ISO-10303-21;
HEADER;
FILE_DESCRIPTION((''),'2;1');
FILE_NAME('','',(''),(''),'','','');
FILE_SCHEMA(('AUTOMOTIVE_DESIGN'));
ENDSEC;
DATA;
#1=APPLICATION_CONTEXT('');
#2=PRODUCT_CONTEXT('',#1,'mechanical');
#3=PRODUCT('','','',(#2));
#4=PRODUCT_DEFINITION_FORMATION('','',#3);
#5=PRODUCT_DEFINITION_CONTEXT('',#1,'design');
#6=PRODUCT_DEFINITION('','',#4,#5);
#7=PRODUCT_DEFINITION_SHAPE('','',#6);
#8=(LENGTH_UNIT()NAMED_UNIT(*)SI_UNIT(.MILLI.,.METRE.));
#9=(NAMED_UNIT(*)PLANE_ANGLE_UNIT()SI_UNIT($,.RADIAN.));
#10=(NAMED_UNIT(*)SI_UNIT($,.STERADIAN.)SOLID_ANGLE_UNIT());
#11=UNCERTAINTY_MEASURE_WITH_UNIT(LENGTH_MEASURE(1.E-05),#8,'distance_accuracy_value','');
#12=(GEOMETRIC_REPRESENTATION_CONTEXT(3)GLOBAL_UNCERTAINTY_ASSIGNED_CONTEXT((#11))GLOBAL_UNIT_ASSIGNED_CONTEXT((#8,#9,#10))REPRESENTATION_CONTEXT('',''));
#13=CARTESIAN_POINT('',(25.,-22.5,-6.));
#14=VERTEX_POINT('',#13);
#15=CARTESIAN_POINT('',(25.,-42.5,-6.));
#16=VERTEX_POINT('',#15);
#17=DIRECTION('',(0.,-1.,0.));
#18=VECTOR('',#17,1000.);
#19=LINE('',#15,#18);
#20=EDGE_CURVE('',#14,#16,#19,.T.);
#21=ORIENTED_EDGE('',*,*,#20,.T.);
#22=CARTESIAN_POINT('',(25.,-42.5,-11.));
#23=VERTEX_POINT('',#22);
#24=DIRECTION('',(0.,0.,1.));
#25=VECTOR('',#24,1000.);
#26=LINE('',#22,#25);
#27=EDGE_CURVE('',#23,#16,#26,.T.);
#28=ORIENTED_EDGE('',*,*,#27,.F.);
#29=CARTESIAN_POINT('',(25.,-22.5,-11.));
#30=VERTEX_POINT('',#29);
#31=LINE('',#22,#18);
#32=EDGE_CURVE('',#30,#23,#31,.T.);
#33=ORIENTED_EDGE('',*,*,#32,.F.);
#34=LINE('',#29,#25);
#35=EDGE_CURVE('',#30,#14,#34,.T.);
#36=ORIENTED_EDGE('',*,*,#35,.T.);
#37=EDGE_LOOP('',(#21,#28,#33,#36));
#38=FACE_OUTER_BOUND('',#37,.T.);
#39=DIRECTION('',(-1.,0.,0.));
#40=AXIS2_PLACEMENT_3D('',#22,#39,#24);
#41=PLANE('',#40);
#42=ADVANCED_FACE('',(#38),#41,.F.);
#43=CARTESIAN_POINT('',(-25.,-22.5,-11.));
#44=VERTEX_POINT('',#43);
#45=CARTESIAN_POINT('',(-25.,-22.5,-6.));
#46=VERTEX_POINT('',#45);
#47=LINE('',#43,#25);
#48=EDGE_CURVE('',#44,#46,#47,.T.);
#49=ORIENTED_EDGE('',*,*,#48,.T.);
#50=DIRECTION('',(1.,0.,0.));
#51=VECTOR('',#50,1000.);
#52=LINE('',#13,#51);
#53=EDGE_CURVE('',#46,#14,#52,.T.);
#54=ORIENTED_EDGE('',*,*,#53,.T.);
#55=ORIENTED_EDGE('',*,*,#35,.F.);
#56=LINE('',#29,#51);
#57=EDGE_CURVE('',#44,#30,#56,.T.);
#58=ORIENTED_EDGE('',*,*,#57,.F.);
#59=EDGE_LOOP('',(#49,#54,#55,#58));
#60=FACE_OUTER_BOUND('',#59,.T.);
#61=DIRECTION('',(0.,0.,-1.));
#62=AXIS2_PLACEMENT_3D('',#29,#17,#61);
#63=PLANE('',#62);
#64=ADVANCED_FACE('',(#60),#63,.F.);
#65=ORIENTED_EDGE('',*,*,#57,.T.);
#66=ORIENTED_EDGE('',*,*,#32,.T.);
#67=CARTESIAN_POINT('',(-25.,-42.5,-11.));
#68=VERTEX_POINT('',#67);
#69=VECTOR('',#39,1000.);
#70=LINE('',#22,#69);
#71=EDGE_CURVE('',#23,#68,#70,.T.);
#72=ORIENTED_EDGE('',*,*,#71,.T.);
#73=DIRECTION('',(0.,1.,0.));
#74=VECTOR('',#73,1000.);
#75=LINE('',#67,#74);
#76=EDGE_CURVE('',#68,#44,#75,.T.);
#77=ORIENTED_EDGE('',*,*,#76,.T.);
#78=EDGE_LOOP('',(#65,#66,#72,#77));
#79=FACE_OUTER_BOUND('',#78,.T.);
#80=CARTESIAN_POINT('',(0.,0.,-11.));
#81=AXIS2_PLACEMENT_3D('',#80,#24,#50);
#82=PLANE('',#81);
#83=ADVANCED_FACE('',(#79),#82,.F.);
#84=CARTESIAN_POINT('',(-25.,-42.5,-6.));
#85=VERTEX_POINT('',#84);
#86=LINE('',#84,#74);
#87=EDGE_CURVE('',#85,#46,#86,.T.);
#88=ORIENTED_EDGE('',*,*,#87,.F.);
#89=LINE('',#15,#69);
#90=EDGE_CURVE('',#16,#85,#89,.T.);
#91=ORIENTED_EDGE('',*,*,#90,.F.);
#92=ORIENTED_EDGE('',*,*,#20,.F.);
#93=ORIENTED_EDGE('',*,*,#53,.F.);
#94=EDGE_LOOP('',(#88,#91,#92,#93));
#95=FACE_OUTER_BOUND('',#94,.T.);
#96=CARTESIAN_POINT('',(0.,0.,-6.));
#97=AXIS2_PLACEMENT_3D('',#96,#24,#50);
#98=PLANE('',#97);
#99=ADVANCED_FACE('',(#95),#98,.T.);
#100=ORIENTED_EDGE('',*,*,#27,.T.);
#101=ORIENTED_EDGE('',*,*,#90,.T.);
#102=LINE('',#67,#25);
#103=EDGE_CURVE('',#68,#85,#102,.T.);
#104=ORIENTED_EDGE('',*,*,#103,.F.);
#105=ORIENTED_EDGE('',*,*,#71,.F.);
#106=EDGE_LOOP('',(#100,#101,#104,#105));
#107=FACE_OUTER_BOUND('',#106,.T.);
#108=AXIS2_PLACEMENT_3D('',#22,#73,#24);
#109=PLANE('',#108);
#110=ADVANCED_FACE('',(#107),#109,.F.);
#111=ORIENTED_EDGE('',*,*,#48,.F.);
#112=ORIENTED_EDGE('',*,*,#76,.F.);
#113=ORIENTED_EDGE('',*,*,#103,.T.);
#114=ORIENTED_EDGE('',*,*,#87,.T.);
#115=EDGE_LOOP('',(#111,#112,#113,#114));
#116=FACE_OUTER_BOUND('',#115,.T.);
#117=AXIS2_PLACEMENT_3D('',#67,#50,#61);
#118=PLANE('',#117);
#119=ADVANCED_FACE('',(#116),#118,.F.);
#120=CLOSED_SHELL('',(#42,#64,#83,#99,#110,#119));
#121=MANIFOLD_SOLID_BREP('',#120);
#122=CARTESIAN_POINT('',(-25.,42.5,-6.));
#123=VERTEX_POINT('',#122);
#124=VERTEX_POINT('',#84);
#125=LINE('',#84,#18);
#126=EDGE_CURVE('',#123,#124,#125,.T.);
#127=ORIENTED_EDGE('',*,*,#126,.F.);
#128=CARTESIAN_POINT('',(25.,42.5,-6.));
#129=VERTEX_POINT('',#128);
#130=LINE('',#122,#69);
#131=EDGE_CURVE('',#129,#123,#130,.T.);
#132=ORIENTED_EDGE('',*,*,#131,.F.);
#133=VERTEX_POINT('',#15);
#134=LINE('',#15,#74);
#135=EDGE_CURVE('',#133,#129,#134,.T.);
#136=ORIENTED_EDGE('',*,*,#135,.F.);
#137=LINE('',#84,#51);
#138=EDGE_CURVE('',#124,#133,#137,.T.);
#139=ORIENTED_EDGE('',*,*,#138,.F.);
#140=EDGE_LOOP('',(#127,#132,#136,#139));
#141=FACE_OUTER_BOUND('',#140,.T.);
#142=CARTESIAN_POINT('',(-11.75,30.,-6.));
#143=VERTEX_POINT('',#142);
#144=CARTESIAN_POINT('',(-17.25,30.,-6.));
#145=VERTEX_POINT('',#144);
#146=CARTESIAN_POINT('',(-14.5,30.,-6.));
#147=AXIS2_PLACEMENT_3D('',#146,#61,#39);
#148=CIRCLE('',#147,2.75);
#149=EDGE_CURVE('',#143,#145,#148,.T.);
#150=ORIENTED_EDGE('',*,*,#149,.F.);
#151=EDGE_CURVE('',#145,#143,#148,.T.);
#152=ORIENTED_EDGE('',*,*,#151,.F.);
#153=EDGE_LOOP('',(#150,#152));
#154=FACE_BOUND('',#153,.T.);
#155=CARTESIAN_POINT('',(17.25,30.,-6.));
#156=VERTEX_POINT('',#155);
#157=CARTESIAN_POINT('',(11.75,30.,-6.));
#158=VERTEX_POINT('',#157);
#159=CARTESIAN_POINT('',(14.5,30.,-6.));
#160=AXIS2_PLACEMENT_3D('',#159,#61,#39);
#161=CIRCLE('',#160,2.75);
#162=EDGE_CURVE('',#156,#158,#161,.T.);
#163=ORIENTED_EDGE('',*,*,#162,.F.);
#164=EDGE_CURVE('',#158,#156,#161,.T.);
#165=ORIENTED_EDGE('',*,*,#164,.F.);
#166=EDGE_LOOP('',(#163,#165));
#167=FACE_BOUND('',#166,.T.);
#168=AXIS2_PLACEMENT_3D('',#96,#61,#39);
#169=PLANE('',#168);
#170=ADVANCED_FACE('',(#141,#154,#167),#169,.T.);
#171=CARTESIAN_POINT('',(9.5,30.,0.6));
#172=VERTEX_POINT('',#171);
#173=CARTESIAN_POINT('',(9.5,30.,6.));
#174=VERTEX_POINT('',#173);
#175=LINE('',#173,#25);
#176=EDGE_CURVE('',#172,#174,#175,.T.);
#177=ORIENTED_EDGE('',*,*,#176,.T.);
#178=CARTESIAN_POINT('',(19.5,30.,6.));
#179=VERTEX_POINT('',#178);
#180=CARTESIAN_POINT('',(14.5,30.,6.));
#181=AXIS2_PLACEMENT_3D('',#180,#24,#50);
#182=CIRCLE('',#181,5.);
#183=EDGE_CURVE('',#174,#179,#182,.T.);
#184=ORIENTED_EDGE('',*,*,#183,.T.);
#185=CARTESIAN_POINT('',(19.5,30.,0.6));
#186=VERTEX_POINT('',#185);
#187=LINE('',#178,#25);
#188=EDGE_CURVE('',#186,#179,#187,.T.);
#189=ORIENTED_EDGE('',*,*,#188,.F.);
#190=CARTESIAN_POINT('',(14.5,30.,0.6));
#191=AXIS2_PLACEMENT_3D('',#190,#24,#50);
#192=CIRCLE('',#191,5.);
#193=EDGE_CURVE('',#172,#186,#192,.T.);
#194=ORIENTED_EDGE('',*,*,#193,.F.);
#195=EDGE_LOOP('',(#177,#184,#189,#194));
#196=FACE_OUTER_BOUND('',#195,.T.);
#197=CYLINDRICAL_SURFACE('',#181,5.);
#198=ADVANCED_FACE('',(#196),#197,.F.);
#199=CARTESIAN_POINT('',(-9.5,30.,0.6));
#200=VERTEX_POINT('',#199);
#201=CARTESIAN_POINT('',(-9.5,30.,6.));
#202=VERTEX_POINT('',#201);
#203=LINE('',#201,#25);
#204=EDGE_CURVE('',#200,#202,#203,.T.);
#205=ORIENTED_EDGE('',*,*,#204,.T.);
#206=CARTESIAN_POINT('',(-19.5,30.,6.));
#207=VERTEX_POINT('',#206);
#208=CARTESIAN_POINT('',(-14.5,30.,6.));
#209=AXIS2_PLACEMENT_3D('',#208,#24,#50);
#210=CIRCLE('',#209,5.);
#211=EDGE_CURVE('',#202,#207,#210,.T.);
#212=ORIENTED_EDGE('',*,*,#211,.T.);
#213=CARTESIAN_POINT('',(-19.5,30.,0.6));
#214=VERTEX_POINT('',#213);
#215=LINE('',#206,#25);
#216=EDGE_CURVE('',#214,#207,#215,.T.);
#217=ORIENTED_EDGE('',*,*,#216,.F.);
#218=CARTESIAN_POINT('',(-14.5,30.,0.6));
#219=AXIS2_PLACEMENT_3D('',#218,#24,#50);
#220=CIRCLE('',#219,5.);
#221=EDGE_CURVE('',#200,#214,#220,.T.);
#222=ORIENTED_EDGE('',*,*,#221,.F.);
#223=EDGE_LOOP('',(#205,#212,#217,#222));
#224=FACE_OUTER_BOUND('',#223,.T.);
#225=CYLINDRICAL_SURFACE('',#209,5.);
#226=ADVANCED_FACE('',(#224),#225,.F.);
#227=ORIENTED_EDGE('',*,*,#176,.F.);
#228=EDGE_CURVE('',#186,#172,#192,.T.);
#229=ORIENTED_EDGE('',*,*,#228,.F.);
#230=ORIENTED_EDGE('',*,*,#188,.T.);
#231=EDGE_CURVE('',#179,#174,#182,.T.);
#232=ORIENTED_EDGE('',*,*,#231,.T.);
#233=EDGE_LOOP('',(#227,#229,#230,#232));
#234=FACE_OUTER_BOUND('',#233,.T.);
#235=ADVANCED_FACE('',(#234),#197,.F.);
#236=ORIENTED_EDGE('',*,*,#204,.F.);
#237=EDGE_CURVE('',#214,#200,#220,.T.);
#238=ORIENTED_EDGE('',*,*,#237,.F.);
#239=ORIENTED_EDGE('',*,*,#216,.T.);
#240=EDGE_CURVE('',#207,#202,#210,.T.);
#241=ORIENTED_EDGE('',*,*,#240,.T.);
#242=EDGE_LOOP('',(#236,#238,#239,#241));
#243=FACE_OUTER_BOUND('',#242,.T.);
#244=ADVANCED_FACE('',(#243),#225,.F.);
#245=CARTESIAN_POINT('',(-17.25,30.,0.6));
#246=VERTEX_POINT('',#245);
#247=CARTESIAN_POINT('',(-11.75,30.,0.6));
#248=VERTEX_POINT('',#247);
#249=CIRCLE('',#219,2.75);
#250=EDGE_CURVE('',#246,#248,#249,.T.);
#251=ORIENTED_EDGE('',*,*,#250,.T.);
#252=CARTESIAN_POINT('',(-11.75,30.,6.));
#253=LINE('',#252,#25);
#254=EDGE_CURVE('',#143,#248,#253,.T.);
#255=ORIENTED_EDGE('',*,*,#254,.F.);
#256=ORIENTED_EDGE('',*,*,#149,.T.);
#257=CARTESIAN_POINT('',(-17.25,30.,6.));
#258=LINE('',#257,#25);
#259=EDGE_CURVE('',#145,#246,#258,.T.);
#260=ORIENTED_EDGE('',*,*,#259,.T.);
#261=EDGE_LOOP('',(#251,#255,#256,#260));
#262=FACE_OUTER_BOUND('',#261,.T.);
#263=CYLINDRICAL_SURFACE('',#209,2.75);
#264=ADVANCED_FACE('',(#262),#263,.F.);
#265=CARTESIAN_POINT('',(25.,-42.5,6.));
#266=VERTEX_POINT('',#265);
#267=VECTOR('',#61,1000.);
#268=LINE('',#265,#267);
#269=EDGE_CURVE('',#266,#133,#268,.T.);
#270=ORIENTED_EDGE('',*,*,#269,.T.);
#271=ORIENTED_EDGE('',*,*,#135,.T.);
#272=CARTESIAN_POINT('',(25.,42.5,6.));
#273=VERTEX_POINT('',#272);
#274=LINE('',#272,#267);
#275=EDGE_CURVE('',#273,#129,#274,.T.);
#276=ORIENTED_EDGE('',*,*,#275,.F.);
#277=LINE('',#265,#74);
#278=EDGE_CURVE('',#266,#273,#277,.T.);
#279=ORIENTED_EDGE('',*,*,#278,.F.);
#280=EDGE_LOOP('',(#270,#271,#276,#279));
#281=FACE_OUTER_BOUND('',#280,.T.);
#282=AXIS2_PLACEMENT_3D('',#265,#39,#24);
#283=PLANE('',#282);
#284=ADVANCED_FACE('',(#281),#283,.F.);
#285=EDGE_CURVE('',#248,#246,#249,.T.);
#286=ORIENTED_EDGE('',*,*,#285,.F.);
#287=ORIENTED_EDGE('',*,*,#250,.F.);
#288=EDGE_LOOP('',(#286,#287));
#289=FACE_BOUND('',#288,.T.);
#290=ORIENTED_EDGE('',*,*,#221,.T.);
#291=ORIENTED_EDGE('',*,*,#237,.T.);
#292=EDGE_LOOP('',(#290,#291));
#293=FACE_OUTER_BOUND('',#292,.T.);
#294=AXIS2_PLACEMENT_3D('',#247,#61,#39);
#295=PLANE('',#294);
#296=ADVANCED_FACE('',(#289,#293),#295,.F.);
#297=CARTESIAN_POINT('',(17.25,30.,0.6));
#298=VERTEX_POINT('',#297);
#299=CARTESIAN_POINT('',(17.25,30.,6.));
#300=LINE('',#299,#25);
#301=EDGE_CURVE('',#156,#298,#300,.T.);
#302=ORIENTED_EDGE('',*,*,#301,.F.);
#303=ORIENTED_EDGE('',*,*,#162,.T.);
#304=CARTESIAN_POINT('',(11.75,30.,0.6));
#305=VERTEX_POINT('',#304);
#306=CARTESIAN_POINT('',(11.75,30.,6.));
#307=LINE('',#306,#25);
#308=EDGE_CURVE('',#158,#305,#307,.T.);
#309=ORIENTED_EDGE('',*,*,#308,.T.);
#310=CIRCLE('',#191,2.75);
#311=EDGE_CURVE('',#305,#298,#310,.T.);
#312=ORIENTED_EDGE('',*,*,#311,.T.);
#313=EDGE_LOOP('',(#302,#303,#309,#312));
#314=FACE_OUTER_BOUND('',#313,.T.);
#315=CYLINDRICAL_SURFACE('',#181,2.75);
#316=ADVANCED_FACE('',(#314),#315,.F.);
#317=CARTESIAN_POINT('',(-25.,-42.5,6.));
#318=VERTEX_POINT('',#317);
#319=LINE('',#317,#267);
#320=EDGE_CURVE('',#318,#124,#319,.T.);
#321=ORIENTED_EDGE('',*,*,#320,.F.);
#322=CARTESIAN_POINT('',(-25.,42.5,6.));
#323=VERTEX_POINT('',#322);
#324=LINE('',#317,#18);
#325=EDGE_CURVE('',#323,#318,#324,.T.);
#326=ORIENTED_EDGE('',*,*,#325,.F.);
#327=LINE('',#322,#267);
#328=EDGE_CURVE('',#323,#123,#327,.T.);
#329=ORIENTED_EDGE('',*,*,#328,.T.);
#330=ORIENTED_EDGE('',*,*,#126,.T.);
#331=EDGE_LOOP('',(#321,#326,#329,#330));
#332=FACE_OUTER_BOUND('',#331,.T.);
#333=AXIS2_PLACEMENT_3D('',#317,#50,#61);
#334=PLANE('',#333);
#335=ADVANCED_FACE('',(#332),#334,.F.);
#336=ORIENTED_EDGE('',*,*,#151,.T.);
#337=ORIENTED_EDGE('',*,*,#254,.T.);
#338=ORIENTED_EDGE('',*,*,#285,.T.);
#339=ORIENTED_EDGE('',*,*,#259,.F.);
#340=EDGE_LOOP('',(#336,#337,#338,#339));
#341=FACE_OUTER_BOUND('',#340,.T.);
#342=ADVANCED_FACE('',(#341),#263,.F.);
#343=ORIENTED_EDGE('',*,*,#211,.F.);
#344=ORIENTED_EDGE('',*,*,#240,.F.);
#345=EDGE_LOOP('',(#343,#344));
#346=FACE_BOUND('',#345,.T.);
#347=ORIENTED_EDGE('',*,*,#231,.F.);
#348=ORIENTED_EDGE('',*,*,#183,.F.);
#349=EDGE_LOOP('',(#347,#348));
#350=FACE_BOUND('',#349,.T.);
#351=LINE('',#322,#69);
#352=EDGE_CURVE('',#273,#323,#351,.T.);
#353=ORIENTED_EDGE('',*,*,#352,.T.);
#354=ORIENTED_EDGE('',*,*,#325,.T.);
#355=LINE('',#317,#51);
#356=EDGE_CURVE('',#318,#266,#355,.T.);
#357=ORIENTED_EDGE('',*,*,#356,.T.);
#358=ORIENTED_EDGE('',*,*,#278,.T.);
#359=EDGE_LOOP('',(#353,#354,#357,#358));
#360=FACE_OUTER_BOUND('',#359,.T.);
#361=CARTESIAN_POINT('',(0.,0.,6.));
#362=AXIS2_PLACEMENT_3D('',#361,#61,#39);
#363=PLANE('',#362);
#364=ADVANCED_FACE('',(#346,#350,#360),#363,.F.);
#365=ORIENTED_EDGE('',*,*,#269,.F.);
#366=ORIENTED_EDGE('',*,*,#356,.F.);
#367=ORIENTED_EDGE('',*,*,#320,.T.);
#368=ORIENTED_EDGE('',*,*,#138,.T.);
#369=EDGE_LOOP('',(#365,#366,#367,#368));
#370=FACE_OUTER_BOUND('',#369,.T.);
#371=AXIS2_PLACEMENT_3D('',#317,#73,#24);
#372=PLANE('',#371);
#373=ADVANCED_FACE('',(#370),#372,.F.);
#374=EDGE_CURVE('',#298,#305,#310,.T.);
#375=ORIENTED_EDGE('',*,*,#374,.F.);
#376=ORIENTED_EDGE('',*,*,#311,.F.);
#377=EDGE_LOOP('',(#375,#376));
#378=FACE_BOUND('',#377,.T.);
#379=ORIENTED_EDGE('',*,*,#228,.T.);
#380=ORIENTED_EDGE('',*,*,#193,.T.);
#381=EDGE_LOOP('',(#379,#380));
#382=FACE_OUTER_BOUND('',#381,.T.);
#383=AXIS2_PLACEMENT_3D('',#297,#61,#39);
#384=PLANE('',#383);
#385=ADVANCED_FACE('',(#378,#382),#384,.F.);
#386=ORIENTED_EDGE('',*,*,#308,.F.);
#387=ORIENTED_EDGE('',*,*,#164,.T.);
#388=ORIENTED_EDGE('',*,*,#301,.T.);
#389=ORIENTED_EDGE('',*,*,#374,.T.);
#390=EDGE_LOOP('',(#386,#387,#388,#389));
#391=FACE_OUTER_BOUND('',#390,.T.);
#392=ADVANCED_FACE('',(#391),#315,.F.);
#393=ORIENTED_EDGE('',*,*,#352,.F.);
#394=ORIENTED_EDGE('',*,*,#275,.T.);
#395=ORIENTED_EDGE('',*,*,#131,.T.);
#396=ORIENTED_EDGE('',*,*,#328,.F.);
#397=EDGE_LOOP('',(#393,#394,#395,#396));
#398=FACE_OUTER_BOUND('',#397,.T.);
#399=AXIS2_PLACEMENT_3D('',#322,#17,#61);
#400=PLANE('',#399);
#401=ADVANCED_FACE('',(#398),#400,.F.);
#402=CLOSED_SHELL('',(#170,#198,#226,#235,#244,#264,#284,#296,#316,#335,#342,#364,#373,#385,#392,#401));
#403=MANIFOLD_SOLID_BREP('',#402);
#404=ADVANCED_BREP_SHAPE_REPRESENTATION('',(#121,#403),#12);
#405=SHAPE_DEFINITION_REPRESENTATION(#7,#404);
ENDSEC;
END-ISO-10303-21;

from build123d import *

# Parameters (mm, degrees)
SKETCH_1_W               = 50
SKETCH_1_H               = 85
EXTRUDE_1_DEPTH          = 6
SKETCH_2_W               = 50
SKETCH_2_H               = 20
EXTRUDE_2_DEPTH          = 5
HOLE_WIZARD_1_AT_2_COUNT = 2
HOLE_WIZARD_1_AT_2_PITCH = 29


with BuildPart() as part:
    # 草图1 → 凸台-拉伸1 (new, symmetric)
    with BuildSketch(Plane.XY):
        Rectangle(SKETCH_1_W, SKETCH_1_H)
    extrude(amount=EXTRUDE_1_DEPTH, both=True)

    # 草图3 → 打孔尺寸(%根据)内六角圆柱头螺钉的类型1 (revolve, cut)
    with BuildSketch(Plane(origin=(-14.5, 30, 6), x_dir=(0, -1, 0), z_dir=(1, 0, 0))):
        Polygon((0, 0), (0, 17), (2.75, 17), (2.75, 5.4), (5, 5.4), (5, 0), align=None)
    hole_wizard_1 = revolve(axis=Axis((-14.5, 30, 12.35), (0, 0, -1)), mode=Mode.SUBTRACT)

    # 打孔尺寸(%根据)内六角圆柱头螺钉的类型1 at 2: 打孔尺寸(%根据)内六角圆柱头螺钉的类型1 ×2
    with Locations(*[(i * HOLE_WIZARD_1_AT_2_PITCH, 0, 0) for i in range(1, HOLE_WIZARD_1_AT_2_COUNT)]):
        add(hole_wizard_1, mode=Mode.SUBTRACT)


with BuildPart() as body_2:
    # 草图2 → 凸台-拉伸2 (new body)
    with BuildSketch(Plane(origin=(0, 0, -6), x_dir=(-1, 0, 0), z_dir=(0, 0, -1))):
        with Locations((0, -32.5)):
            Rectangle(SKETCH_2_W, SKETCH_2_H)
    extrude(amount=EXTRUDE_2_DEPTH)


solid = Compound([part.part, body_2.part])
